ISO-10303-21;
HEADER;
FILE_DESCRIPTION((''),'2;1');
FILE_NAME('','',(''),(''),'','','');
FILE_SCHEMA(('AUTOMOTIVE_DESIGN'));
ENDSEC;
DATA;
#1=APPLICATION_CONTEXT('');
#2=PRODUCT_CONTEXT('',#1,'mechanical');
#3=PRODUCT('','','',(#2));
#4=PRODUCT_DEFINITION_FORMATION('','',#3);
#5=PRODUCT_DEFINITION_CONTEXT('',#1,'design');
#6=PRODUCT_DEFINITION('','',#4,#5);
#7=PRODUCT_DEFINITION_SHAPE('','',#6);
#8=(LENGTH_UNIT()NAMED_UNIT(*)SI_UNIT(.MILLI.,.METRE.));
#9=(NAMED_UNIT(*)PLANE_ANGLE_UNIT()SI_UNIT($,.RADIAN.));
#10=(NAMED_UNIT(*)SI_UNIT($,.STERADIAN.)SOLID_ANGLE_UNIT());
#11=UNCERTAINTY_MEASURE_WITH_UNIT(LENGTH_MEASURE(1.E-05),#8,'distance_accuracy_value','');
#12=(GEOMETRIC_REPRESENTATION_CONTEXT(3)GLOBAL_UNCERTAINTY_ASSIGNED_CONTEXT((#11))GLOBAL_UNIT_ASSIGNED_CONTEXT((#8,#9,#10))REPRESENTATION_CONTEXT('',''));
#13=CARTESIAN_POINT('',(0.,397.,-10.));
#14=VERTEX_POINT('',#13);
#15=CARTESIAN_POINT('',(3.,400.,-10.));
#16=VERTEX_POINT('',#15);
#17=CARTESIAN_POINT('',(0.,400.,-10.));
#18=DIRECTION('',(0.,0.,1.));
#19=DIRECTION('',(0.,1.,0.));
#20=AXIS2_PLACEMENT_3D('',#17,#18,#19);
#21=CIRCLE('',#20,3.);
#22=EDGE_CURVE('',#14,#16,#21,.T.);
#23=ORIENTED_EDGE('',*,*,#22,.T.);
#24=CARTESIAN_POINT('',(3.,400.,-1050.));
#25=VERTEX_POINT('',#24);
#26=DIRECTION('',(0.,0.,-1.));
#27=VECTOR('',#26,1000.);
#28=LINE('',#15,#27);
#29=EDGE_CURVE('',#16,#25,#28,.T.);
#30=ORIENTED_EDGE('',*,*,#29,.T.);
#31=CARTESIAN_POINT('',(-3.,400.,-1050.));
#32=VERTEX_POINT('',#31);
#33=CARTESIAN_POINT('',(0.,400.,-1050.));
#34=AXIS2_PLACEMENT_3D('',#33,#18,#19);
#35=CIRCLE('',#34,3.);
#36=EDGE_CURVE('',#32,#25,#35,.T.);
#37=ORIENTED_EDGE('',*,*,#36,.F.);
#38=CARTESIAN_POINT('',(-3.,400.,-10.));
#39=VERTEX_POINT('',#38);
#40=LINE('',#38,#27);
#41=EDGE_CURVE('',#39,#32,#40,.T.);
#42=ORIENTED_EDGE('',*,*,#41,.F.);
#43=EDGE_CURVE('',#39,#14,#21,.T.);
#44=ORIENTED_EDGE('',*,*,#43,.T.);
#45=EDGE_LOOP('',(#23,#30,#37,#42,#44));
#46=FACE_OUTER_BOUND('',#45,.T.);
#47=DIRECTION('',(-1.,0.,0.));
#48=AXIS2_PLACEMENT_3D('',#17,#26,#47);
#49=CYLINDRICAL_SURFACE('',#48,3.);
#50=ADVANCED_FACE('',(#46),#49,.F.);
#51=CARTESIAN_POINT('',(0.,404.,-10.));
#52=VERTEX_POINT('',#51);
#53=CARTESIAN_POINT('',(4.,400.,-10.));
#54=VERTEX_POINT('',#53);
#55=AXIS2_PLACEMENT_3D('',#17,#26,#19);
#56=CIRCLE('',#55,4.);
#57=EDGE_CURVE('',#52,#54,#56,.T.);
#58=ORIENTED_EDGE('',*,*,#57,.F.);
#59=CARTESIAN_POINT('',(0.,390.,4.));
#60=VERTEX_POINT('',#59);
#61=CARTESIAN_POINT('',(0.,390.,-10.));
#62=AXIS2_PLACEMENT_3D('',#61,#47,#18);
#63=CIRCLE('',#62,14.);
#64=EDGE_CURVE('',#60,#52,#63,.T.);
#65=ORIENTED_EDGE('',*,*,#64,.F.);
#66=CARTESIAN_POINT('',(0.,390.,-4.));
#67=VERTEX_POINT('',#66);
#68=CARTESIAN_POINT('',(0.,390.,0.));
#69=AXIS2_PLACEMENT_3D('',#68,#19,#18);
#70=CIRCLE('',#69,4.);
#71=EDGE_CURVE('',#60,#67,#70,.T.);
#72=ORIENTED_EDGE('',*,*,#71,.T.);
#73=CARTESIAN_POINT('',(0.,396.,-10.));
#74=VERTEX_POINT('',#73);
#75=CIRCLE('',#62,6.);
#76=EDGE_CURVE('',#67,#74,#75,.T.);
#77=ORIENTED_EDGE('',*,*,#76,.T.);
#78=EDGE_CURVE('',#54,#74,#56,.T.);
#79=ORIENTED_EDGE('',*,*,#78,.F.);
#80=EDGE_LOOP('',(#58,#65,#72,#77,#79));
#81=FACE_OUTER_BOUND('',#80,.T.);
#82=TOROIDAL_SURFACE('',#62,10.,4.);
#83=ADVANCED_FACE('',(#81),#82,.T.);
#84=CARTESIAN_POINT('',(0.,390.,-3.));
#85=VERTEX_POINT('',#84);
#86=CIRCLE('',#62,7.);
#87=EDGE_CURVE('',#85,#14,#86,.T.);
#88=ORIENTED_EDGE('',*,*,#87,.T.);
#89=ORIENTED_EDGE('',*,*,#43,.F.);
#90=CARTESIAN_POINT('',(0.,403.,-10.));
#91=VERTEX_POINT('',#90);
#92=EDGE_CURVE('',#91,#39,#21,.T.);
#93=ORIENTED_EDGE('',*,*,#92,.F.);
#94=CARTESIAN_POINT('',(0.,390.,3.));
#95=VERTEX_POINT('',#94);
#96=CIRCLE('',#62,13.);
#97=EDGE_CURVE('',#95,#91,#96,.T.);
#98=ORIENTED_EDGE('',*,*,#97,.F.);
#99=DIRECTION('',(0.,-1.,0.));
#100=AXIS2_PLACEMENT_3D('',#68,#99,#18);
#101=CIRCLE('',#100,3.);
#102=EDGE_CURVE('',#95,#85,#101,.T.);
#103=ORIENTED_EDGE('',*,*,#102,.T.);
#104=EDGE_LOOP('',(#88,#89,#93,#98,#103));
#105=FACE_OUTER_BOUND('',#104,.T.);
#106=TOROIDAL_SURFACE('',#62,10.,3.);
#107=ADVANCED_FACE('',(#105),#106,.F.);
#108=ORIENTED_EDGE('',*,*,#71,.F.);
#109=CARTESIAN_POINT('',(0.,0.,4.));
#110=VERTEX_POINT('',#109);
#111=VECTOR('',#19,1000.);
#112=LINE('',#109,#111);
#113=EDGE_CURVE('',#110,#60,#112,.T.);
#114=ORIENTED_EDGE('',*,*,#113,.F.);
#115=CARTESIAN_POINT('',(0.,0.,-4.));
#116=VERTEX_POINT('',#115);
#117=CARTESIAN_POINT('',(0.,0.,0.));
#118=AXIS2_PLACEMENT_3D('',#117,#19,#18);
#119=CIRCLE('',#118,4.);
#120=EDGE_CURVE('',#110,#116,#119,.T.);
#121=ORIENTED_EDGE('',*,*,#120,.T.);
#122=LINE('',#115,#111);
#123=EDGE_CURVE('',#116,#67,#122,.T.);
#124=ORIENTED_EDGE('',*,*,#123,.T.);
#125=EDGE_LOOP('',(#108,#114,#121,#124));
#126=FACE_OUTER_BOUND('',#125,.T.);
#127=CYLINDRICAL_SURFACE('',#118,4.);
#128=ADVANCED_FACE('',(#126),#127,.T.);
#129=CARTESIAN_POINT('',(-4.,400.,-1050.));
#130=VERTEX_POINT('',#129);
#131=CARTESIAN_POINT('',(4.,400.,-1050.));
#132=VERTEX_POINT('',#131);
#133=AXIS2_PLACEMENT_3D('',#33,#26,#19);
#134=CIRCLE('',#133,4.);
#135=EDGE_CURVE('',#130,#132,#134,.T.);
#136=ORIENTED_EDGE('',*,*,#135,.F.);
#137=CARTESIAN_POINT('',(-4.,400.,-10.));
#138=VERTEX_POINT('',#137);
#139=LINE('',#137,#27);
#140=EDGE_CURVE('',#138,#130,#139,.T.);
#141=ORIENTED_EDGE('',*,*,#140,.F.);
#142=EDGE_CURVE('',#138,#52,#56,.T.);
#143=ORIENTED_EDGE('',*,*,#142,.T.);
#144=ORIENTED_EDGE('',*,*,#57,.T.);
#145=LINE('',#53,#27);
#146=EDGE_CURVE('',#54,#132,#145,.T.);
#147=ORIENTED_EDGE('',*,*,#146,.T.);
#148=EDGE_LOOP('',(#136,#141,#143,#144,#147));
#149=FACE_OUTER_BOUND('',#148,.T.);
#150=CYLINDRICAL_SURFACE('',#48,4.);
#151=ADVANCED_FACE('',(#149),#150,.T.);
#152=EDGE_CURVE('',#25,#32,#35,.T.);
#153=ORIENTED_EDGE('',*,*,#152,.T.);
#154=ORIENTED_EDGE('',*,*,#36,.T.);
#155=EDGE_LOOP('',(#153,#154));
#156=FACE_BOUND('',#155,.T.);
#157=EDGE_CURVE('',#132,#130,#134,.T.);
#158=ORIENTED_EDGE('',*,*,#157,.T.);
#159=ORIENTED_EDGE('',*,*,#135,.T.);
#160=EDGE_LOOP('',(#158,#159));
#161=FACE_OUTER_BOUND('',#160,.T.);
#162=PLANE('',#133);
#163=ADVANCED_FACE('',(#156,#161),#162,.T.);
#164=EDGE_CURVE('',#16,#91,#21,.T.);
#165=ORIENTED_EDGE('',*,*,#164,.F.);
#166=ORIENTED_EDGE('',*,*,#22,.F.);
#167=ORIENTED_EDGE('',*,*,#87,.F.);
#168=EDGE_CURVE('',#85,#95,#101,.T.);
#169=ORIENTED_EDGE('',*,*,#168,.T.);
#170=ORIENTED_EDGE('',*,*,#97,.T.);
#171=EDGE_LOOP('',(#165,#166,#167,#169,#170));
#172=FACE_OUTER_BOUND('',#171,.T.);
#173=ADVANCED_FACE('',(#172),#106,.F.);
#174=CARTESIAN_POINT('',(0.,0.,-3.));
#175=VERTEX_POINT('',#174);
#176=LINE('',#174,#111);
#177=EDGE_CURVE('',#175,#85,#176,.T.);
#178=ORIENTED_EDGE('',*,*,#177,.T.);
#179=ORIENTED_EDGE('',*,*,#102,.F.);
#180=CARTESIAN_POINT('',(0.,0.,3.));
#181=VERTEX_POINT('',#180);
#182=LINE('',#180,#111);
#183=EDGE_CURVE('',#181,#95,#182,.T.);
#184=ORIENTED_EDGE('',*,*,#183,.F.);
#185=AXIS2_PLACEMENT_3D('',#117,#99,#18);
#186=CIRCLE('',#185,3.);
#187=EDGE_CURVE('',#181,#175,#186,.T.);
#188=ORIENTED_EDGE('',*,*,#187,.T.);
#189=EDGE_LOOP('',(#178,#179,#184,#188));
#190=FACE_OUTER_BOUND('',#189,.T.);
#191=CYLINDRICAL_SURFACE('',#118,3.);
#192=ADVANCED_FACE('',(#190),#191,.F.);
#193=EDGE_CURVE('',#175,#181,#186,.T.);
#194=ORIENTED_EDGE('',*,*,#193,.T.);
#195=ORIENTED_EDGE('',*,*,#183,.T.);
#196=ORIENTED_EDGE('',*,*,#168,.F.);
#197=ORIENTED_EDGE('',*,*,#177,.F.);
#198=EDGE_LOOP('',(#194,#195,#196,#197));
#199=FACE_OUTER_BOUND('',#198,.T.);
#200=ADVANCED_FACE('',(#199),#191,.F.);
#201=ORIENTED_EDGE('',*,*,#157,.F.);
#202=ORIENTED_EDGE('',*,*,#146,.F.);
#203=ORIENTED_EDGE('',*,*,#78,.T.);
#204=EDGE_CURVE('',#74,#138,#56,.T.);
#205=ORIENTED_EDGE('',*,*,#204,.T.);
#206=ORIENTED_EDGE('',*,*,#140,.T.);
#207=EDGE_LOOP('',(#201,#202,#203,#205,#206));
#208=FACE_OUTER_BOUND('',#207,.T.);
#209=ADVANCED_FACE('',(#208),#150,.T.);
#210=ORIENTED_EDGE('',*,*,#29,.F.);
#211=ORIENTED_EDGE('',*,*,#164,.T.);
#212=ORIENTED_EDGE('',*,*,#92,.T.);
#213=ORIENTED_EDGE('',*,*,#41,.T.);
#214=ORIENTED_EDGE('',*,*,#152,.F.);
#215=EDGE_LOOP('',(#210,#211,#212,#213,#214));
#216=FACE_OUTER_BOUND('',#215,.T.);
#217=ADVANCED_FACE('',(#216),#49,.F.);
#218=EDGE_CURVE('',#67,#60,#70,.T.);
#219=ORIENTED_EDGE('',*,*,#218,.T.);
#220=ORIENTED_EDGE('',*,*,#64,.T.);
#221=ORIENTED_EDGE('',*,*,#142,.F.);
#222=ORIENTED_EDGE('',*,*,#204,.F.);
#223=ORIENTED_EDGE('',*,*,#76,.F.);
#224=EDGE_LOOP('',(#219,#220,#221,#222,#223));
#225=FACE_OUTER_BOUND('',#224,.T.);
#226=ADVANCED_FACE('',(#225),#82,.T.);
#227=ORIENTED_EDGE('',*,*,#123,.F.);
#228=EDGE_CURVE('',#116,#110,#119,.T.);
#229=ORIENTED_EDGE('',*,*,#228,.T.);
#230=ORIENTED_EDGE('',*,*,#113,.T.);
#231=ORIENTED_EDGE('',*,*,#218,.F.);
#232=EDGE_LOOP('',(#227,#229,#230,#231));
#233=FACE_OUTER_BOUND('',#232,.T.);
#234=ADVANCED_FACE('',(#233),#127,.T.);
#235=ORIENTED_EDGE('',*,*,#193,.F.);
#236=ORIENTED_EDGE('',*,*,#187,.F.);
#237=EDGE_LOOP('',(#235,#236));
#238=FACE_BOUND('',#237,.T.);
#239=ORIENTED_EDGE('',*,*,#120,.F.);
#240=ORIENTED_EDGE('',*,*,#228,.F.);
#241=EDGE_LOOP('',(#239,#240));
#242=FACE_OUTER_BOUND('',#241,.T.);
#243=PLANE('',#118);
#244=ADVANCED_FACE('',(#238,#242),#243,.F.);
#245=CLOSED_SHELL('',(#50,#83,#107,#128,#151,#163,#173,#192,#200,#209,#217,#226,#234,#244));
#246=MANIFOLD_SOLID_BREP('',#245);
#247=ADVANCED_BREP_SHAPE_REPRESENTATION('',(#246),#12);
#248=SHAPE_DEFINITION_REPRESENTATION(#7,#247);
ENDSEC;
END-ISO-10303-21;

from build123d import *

# Parameters (mm, degrees)
SKETCH1_R   = 4
SKETCH1_R_2 = 3


with BuildPart() as part:
    # Sweep1: sweep along a path in Sketch2
    with BuildLine(Plane(origin=(0, 0, 0), x_dir=(0, 0, -1), z_dir=(1, 0, 0))) as sweep1_path:
        Line((0, 0), (0, 390))
        ThreePointArc((0, 390), (2.928932188, 397.071067812), (10, 400))
        Line((10, 400), (1050, 400))
    # Sketch1 → Sweep1 (sweep)
    with BuildSketch(Plane(origin=(0, 0, 0), x_dir=(1, 0, 0), z_dir=(0, 1, 0))):
        Circle(SKETCH1_R)
        Circle(SKETCH1_R_2, mode=Mode.SUBTRACT)
    sweep(path=sweep1_path.line)


solid = part.part
